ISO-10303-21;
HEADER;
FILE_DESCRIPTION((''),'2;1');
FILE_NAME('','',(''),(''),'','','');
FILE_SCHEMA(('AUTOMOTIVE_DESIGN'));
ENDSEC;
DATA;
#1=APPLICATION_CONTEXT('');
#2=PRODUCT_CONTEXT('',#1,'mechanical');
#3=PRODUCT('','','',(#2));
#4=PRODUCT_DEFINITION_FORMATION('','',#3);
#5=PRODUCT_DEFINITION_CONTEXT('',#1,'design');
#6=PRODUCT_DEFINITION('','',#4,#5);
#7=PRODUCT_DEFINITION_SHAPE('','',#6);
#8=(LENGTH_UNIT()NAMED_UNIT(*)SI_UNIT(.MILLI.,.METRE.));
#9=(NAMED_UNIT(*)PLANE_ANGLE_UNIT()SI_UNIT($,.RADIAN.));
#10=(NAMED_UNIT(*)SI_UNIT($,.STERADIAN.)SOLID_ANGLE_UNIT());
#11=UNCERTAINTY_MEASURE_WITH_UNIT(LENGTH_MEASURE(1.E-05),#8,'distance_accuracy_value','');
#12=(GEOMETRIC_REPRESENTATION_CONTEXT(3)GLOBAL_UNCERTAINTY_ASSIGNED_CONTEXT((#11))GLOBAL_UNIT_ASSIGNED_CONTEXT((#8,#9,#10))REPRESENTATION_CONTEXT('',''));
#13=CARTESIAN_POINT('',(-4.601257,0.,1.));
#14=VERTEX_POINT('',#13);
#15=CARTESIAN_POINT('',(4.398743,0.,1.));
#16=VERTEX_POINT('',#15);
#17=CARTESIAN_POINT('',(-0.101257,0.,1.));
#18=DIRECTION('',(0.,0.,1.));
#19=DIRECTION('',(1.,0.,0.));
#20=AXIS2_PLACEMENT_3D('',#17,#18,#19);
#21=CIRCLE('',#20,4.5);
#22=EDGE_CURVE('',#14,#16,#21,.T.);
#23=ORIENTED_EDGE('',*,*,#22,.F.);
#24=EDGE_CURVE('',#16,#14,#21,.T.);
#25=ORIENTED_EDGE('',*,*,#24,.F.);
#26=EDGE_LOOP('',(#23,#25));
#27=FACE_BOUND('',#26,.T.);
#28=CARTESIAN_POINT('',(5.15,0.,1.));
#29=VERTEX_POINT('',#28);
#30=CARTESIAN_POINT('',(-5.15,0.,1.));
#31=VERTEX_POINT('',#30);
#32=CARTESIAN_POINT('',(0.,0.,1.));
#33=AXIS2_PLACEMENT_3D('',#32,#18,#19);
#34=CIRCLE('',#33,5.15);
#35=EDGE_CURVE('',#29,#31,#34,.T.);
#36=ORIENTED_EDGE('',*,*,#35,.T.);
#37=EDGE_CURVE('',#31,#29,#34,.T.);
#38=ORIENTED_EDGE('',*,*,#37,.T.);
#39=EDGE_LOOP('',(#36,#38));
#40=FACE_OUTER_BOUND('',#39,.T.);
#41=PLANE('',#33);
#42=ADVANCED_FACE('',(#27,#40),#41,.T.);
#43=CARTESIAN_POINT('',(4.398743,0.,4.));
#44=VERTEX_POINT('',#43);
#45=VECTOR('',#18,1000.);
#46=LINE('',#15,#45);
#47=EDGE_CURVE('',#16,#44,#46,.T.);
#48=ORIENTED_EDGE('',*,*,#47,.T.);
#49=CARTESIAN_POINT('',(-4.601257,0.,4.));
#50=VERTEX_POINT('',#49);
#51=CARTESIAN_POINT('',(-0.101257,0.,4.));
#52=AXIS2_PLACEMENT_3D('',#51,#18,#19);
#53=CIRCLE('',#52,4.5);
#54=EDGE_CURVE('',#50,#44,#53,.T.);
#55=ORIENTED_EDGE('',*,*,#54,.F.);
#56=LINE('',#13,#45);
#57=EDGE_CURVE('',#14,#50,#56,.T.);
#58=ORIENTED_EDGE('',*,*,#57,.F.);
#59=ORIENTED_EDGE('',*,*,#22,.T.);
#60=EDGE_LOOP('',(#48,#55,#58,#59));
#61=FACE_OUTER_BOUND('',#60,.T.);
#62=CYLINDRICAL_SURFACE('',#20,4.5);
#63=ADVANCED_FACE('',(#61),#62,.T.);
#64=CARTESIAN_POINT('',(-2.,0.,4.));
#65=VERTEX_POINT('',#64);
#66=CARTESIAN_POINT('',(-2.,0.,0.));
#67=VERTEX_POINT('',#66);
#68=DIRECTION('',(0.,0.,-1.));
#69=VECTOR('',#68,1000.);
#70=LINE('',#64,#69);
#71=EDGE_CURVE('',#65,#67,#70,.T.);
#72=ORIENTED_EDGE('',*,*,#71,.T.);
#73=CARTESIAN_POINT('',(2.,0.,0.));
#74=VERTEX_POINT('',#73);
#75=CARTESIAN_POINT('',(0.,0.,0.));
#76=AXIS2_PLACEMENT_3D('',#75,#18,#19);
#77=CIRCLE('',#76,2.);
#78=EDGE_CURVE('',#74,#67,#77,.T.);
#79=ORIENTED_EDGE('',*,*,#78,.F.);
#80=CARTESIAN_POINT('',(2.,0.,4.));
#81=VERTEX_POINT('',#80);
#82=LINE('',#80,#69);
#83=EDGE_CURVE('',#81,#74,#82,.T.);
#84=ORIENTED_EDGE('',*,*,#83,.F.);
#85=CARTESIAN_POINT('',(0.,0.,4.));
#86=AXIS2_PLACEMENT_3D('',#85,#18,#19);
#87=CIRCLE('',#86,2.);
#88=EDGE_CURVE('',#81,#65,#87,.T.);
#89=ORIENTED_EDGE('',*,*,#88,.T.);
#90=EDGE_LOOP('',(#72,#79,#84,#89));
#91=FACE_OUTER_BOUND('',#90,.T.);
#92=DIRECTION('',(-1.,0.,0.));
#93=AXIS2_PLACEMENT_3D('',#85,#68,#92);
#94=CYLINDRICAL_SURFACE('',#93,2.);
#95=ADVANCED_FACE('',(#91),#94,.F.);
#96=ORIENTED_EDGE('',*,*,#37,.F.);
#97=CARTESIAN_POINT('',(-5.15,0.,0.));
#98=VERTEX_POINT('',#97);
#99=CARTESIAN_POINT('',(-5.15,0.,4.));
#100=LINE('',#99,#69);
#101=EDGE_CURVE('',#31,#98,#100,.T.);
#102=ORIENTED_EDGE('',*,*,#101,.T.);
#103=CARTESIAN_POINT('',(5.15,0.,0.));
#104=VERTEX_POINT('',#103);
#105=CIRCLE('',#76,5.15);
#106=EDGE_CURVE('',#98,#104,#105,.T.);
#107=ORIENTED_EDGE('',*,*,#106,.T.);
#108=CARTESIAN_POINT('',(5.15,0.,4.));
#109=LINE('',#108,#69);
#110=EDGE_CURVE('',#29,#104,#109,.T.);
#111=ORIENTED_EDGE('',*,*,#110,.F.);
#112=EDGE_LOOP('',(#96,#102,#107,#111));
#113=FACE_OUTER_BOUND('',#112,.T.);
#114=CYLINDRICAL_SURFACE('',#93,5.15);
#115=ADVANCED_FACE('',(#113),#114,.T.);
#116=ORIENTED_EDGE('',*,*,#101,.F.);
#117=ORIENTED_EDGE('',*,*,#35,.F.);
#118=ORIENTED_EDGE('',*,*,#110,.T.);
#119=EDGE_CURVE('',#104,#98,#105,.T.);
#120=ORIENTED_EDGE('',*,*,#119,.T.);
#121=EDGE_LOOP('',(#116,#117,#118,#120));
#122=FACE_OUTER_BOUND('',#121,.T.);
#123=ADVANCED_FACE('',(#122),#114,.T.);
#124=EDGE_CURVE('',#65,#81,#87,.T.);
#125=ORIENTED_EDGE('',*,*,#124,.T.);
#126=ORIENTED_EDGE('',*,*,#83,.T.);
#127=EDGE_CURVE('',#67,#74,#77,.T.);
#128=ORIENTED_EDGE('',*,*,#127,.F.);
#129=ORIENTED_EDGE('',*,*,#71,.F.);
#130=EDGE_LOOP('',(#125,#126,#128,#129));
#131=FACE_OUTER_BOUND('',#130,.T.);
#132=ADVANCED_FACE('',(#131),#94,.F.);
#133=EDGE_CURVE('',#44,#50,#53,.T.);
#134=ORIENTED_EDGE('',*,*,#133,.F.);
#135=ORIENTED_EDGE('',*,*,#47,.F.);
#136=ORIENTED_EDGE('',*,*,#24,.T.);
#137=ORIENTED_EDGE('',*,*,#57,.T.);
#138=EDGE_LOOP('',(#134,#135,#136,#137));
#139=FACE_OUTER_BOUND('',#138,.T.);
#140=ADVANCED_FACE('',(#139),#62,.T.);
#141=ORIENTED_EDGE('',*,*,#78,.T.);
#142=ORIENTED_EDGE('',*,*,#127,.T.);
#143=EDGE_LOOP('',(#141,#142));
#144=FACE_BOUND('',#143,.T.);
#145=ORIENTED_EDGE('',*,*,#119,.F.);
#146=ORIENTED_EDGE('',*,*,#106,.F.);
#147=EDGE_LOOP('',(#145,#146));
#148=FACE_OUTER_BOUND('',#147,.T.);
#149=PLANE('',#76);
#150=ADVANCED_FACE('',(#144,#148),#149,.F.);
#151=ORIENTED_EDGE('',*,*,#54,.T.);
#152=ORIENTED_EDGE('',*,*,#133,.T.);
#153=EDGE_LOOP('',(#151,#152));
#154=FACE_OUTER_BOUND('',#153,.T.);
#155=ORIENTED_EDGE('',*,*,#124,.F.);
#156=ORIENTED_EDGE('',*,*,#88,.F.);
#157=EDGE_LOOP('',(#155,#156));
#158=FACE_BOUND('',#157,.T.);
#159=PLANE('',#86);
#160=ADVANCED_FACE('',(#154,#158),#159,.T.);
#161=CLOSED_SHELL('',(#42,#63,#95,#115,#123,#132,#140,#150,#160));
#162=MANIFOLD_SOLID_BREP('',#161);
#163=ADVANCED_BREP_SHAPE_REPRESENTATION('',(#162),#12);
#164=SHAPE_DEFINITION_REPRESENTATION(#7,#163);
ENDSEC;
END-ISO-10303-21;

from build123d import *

# Parameters (mm, degrees)
SKETCH_1_R          = 5.15
SKETCH_1_R_2        = 2
EXTRUDE_1_DEPTH     = 4
CUT_EXTRUDE_START   = -3
SKETCH_2_R          = 5.15
SKETCH_2_R_2        = 4.5
CUT_EXTRUDE_1_DEPTH = 3


with BuildPart() as part:
    # 草图1 → 凸台-拉伸1 (new body)
    with BuildSketch(Plane.XY):
        Circle(SKETCH_1_R)
        Circle(SKETCH_1_R_2, mode=Mode.SUBTRACT)
    extrude(amount=EXTRUDE_1_DEPTH)

    # 草图2 → 切除-拉伸1 (cut)
    with BuildSketch(Plane.XY.offset(4).offset(CUT_EXTRUDE_START)):
        Circle(SKETCH_2_R)
        with Locations((-0.101257267, 0)):
            Circle(SKETCH_2_R_2, mode=Mode.SUBTRACT)
    extrude(amount=CUT_EXTRUDE_1_DEPTH, mode=Mode.SUBTRACT)


solid = part.part
